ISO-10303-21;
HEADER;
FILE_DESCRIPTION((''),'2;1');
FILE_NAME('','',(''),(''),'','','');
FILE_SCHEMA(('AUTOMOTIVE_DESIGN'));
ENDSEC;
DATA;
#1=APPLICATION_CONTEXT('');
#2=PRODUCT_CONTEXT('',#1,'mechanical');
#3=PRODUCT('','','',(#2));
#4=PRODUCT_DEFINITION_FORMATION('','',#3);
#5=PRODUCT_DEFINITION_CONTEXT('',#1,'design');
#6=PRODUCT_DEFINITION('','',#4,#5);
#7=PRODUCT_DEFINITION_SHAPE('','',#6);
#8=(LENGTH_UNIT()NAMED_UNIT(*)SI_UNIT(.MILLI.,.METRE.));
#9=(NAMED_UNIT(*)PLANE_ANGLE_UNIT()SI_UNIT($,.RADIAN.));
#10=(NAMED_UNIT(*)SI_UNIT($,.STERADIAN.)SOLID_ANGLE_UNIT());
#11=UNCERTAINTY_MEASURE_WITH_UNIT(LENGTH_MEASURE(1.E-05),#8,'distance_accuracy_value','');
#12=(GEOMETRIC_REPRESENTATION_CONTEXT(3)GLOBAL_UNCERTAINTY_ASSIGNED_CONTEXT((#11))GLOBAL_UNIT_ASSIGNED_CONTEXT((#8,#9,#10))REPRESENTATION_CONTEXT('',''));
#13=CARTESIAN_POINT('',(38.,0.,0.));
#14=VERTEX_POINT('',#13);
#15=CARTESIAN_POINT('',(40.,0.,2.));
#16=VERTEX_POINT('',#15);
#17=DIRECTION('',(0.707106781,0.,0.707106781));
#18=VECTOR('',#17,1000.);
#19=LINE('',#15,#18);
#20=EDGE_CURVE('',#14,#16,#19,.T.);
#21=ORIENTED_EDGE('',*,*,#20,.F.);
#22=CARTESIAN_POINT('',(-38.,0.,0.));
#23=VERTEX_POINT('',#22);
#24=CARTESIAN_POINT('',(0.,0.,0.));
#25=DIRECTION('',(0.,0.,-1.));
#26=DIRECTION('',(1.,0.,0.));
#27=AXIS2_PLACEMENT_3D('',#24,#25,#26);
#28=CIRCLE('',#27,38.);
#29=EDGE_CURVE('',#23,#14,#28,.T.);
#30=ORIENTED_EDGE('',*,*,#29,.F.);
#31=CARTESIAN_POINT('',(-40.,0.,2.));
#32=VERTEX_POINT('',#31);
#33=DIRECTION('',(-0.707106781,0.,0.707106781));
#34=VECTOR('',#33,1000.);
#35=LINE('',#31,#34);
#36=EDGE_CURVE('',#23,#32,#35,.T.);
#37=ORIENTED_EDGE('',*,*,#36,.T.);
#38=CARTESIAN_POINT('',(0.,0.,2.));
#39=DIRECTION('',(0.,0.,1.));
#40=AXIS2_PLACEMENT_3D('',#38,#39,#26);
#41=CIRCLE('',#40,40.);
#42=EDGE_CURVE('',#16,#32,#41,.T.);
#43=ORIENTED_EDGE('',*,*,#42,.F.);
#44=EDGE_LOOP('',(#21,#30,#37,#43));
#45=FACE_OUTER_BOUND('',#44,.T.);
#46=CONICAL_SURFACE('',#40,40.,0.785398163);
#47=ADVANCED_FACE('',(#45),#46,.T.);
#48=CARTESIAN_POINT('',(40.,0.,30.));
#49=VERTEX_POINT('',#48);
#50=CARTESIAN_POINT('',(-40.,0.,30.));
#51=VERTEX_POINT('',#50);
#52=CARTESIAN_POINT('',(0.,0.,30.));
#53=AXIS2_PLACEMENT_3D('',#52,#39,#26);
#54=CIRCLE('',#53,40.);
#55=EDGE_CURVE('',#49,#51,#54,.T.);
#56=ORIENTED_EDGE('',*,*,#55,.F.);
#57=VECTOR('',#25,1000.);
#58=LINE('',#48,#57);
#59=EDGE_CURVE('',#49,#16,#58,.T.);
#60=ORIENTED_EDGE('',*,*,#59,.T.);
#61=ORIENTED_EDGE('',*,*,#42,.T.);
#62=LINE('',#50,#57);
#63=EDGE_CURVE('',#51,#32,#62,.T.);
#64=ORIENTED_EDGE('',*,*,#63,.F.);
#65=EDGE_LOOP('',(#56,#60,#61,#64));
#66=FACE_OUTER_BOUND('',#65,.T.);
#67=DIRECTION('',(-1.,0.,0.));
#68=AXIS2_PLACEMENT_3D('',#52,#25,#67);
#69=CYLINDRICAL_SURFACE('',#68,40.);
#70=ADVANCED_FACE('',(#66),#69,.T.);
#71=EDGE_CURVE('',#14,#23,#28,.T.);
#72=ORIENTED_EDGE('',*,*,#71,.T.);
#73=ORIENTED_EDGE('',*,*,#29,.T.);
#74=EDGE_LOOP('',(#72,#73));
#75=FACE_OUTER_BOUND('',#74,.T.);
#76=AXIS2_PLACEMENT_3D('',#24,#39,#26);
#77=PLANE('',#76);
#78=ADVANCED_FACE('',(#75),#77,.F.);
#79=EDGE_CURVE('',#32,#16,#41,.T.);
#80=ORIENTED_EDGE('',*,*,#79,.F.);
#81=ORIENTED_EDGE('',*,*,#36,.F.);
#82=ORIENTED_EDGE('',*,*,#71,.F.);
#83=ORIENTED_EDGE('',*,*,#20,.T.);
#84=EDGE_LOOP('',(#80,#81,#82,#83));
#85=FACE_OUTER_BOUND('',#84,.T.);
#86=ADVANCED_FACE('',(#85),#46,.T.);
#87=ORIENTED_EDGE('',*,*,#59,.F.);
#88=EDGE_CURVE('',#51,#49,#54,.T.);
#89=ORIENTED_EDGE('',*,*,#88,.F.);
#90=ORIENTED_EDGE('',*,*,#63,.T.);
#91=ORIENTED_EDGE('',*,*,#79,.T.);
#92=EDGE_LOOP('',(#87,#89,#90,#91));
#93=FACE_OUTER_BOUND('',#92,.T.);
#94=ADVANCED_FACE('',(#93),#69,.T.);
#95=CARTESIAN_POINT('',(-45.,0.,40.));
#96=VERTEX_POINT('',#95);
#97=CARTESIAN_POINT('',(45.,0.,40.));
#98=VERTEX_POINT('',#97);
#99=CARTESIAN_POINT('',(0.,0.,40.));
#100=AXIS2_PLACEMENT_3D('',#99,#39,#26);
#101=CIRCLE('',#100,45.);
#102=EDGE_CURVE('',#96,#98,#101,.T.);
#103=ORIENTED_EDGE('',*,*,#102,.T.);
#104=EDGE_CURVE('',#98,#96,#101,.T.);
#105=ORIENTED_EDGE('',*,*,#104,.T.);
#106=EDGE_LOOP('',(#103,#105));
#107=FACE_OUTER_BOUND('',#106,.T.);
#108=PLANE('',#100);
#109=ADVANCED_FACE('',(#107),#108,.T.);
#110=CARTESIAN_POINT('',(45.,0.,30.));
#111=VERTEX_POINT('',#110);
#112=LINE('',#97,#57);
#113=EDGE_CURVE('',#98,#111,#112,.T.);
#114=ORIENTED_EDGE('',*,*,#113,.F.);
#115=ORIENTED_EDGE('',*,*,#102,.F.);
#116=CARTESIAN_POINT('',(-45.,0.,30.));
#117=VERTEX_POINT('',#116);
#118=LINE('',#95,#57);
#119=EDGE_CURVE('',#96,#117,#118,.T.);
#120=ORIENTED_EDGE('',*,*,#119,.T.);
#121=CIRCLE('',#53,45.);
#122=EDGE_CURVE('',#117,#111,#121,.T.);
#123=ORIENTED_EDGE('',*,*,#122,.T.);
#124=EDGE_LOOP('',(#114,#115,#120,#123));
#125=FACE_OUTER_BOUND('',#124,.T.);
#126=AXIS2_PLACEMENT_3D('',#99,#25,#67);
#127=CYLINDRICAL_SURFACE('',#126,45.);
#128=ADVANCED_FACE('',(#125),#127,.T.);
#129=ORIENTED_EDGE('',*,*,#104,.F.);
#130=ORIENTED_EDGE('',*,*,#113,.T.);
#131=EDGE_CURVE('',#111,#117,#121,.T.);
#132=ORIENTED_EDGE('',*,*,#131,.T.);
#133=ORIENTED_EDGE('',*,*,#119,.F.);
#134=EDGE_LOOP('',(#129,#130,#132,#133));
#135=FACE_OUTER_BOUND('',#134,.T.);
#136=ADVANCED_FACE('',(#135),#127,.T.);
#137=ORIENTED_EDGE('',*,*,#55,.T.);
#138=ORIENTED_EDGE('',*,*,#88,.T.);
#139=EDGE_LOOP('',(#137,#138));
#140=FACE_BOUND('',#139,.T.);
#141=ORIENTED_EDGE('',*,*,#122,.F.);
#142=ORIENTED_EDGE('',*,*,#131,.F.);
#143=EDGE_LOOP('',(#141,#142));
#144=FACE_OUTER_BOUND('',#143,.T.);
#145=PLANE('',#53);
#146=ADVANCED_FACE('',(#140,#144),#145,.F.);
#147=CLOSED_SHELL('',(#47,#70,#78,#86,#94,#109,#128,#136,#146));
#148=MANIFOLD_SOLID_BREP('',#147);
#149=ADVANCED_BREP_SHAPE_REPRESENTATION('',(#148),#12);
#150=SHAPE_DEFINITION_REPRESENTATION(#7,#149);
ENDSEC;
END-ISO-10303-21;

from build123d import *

# Parameters (mm, degrees)
SKETCH_1_R      = 40
EXTRUDE_1_DEPTH = 30
SKETCH_2_R      = 45
EXTRUDE_2_DEPTH = 10
CHAMFER_1_SIZE  = 2


with BuildPart() as part:
    # 草图1 → 凸台-拉伸1 (new body)
    with BuildSketch(Plane.XY):
        Circle(SKETCH_1_R)
    extrude(amount=EXTRUDE_1_DEPTH)

    # 草图2 → 凸台-拉伸2 (add)
    with BuildSketch(Plane.XY.offset(30)):
        Circle(SKETCH_2_R)
    extrude(amount=EXTRUDE_2_DEPTH)

    # 倒角1
    chamfer_1_edges = [part.edges().sort_by_distance(p)[0] for p in [
        (-40, 0, 0),
    ]]
    chamfer(chamfer_1_edges, length=CHAMFER_1_SIZE)


solid = part.part
